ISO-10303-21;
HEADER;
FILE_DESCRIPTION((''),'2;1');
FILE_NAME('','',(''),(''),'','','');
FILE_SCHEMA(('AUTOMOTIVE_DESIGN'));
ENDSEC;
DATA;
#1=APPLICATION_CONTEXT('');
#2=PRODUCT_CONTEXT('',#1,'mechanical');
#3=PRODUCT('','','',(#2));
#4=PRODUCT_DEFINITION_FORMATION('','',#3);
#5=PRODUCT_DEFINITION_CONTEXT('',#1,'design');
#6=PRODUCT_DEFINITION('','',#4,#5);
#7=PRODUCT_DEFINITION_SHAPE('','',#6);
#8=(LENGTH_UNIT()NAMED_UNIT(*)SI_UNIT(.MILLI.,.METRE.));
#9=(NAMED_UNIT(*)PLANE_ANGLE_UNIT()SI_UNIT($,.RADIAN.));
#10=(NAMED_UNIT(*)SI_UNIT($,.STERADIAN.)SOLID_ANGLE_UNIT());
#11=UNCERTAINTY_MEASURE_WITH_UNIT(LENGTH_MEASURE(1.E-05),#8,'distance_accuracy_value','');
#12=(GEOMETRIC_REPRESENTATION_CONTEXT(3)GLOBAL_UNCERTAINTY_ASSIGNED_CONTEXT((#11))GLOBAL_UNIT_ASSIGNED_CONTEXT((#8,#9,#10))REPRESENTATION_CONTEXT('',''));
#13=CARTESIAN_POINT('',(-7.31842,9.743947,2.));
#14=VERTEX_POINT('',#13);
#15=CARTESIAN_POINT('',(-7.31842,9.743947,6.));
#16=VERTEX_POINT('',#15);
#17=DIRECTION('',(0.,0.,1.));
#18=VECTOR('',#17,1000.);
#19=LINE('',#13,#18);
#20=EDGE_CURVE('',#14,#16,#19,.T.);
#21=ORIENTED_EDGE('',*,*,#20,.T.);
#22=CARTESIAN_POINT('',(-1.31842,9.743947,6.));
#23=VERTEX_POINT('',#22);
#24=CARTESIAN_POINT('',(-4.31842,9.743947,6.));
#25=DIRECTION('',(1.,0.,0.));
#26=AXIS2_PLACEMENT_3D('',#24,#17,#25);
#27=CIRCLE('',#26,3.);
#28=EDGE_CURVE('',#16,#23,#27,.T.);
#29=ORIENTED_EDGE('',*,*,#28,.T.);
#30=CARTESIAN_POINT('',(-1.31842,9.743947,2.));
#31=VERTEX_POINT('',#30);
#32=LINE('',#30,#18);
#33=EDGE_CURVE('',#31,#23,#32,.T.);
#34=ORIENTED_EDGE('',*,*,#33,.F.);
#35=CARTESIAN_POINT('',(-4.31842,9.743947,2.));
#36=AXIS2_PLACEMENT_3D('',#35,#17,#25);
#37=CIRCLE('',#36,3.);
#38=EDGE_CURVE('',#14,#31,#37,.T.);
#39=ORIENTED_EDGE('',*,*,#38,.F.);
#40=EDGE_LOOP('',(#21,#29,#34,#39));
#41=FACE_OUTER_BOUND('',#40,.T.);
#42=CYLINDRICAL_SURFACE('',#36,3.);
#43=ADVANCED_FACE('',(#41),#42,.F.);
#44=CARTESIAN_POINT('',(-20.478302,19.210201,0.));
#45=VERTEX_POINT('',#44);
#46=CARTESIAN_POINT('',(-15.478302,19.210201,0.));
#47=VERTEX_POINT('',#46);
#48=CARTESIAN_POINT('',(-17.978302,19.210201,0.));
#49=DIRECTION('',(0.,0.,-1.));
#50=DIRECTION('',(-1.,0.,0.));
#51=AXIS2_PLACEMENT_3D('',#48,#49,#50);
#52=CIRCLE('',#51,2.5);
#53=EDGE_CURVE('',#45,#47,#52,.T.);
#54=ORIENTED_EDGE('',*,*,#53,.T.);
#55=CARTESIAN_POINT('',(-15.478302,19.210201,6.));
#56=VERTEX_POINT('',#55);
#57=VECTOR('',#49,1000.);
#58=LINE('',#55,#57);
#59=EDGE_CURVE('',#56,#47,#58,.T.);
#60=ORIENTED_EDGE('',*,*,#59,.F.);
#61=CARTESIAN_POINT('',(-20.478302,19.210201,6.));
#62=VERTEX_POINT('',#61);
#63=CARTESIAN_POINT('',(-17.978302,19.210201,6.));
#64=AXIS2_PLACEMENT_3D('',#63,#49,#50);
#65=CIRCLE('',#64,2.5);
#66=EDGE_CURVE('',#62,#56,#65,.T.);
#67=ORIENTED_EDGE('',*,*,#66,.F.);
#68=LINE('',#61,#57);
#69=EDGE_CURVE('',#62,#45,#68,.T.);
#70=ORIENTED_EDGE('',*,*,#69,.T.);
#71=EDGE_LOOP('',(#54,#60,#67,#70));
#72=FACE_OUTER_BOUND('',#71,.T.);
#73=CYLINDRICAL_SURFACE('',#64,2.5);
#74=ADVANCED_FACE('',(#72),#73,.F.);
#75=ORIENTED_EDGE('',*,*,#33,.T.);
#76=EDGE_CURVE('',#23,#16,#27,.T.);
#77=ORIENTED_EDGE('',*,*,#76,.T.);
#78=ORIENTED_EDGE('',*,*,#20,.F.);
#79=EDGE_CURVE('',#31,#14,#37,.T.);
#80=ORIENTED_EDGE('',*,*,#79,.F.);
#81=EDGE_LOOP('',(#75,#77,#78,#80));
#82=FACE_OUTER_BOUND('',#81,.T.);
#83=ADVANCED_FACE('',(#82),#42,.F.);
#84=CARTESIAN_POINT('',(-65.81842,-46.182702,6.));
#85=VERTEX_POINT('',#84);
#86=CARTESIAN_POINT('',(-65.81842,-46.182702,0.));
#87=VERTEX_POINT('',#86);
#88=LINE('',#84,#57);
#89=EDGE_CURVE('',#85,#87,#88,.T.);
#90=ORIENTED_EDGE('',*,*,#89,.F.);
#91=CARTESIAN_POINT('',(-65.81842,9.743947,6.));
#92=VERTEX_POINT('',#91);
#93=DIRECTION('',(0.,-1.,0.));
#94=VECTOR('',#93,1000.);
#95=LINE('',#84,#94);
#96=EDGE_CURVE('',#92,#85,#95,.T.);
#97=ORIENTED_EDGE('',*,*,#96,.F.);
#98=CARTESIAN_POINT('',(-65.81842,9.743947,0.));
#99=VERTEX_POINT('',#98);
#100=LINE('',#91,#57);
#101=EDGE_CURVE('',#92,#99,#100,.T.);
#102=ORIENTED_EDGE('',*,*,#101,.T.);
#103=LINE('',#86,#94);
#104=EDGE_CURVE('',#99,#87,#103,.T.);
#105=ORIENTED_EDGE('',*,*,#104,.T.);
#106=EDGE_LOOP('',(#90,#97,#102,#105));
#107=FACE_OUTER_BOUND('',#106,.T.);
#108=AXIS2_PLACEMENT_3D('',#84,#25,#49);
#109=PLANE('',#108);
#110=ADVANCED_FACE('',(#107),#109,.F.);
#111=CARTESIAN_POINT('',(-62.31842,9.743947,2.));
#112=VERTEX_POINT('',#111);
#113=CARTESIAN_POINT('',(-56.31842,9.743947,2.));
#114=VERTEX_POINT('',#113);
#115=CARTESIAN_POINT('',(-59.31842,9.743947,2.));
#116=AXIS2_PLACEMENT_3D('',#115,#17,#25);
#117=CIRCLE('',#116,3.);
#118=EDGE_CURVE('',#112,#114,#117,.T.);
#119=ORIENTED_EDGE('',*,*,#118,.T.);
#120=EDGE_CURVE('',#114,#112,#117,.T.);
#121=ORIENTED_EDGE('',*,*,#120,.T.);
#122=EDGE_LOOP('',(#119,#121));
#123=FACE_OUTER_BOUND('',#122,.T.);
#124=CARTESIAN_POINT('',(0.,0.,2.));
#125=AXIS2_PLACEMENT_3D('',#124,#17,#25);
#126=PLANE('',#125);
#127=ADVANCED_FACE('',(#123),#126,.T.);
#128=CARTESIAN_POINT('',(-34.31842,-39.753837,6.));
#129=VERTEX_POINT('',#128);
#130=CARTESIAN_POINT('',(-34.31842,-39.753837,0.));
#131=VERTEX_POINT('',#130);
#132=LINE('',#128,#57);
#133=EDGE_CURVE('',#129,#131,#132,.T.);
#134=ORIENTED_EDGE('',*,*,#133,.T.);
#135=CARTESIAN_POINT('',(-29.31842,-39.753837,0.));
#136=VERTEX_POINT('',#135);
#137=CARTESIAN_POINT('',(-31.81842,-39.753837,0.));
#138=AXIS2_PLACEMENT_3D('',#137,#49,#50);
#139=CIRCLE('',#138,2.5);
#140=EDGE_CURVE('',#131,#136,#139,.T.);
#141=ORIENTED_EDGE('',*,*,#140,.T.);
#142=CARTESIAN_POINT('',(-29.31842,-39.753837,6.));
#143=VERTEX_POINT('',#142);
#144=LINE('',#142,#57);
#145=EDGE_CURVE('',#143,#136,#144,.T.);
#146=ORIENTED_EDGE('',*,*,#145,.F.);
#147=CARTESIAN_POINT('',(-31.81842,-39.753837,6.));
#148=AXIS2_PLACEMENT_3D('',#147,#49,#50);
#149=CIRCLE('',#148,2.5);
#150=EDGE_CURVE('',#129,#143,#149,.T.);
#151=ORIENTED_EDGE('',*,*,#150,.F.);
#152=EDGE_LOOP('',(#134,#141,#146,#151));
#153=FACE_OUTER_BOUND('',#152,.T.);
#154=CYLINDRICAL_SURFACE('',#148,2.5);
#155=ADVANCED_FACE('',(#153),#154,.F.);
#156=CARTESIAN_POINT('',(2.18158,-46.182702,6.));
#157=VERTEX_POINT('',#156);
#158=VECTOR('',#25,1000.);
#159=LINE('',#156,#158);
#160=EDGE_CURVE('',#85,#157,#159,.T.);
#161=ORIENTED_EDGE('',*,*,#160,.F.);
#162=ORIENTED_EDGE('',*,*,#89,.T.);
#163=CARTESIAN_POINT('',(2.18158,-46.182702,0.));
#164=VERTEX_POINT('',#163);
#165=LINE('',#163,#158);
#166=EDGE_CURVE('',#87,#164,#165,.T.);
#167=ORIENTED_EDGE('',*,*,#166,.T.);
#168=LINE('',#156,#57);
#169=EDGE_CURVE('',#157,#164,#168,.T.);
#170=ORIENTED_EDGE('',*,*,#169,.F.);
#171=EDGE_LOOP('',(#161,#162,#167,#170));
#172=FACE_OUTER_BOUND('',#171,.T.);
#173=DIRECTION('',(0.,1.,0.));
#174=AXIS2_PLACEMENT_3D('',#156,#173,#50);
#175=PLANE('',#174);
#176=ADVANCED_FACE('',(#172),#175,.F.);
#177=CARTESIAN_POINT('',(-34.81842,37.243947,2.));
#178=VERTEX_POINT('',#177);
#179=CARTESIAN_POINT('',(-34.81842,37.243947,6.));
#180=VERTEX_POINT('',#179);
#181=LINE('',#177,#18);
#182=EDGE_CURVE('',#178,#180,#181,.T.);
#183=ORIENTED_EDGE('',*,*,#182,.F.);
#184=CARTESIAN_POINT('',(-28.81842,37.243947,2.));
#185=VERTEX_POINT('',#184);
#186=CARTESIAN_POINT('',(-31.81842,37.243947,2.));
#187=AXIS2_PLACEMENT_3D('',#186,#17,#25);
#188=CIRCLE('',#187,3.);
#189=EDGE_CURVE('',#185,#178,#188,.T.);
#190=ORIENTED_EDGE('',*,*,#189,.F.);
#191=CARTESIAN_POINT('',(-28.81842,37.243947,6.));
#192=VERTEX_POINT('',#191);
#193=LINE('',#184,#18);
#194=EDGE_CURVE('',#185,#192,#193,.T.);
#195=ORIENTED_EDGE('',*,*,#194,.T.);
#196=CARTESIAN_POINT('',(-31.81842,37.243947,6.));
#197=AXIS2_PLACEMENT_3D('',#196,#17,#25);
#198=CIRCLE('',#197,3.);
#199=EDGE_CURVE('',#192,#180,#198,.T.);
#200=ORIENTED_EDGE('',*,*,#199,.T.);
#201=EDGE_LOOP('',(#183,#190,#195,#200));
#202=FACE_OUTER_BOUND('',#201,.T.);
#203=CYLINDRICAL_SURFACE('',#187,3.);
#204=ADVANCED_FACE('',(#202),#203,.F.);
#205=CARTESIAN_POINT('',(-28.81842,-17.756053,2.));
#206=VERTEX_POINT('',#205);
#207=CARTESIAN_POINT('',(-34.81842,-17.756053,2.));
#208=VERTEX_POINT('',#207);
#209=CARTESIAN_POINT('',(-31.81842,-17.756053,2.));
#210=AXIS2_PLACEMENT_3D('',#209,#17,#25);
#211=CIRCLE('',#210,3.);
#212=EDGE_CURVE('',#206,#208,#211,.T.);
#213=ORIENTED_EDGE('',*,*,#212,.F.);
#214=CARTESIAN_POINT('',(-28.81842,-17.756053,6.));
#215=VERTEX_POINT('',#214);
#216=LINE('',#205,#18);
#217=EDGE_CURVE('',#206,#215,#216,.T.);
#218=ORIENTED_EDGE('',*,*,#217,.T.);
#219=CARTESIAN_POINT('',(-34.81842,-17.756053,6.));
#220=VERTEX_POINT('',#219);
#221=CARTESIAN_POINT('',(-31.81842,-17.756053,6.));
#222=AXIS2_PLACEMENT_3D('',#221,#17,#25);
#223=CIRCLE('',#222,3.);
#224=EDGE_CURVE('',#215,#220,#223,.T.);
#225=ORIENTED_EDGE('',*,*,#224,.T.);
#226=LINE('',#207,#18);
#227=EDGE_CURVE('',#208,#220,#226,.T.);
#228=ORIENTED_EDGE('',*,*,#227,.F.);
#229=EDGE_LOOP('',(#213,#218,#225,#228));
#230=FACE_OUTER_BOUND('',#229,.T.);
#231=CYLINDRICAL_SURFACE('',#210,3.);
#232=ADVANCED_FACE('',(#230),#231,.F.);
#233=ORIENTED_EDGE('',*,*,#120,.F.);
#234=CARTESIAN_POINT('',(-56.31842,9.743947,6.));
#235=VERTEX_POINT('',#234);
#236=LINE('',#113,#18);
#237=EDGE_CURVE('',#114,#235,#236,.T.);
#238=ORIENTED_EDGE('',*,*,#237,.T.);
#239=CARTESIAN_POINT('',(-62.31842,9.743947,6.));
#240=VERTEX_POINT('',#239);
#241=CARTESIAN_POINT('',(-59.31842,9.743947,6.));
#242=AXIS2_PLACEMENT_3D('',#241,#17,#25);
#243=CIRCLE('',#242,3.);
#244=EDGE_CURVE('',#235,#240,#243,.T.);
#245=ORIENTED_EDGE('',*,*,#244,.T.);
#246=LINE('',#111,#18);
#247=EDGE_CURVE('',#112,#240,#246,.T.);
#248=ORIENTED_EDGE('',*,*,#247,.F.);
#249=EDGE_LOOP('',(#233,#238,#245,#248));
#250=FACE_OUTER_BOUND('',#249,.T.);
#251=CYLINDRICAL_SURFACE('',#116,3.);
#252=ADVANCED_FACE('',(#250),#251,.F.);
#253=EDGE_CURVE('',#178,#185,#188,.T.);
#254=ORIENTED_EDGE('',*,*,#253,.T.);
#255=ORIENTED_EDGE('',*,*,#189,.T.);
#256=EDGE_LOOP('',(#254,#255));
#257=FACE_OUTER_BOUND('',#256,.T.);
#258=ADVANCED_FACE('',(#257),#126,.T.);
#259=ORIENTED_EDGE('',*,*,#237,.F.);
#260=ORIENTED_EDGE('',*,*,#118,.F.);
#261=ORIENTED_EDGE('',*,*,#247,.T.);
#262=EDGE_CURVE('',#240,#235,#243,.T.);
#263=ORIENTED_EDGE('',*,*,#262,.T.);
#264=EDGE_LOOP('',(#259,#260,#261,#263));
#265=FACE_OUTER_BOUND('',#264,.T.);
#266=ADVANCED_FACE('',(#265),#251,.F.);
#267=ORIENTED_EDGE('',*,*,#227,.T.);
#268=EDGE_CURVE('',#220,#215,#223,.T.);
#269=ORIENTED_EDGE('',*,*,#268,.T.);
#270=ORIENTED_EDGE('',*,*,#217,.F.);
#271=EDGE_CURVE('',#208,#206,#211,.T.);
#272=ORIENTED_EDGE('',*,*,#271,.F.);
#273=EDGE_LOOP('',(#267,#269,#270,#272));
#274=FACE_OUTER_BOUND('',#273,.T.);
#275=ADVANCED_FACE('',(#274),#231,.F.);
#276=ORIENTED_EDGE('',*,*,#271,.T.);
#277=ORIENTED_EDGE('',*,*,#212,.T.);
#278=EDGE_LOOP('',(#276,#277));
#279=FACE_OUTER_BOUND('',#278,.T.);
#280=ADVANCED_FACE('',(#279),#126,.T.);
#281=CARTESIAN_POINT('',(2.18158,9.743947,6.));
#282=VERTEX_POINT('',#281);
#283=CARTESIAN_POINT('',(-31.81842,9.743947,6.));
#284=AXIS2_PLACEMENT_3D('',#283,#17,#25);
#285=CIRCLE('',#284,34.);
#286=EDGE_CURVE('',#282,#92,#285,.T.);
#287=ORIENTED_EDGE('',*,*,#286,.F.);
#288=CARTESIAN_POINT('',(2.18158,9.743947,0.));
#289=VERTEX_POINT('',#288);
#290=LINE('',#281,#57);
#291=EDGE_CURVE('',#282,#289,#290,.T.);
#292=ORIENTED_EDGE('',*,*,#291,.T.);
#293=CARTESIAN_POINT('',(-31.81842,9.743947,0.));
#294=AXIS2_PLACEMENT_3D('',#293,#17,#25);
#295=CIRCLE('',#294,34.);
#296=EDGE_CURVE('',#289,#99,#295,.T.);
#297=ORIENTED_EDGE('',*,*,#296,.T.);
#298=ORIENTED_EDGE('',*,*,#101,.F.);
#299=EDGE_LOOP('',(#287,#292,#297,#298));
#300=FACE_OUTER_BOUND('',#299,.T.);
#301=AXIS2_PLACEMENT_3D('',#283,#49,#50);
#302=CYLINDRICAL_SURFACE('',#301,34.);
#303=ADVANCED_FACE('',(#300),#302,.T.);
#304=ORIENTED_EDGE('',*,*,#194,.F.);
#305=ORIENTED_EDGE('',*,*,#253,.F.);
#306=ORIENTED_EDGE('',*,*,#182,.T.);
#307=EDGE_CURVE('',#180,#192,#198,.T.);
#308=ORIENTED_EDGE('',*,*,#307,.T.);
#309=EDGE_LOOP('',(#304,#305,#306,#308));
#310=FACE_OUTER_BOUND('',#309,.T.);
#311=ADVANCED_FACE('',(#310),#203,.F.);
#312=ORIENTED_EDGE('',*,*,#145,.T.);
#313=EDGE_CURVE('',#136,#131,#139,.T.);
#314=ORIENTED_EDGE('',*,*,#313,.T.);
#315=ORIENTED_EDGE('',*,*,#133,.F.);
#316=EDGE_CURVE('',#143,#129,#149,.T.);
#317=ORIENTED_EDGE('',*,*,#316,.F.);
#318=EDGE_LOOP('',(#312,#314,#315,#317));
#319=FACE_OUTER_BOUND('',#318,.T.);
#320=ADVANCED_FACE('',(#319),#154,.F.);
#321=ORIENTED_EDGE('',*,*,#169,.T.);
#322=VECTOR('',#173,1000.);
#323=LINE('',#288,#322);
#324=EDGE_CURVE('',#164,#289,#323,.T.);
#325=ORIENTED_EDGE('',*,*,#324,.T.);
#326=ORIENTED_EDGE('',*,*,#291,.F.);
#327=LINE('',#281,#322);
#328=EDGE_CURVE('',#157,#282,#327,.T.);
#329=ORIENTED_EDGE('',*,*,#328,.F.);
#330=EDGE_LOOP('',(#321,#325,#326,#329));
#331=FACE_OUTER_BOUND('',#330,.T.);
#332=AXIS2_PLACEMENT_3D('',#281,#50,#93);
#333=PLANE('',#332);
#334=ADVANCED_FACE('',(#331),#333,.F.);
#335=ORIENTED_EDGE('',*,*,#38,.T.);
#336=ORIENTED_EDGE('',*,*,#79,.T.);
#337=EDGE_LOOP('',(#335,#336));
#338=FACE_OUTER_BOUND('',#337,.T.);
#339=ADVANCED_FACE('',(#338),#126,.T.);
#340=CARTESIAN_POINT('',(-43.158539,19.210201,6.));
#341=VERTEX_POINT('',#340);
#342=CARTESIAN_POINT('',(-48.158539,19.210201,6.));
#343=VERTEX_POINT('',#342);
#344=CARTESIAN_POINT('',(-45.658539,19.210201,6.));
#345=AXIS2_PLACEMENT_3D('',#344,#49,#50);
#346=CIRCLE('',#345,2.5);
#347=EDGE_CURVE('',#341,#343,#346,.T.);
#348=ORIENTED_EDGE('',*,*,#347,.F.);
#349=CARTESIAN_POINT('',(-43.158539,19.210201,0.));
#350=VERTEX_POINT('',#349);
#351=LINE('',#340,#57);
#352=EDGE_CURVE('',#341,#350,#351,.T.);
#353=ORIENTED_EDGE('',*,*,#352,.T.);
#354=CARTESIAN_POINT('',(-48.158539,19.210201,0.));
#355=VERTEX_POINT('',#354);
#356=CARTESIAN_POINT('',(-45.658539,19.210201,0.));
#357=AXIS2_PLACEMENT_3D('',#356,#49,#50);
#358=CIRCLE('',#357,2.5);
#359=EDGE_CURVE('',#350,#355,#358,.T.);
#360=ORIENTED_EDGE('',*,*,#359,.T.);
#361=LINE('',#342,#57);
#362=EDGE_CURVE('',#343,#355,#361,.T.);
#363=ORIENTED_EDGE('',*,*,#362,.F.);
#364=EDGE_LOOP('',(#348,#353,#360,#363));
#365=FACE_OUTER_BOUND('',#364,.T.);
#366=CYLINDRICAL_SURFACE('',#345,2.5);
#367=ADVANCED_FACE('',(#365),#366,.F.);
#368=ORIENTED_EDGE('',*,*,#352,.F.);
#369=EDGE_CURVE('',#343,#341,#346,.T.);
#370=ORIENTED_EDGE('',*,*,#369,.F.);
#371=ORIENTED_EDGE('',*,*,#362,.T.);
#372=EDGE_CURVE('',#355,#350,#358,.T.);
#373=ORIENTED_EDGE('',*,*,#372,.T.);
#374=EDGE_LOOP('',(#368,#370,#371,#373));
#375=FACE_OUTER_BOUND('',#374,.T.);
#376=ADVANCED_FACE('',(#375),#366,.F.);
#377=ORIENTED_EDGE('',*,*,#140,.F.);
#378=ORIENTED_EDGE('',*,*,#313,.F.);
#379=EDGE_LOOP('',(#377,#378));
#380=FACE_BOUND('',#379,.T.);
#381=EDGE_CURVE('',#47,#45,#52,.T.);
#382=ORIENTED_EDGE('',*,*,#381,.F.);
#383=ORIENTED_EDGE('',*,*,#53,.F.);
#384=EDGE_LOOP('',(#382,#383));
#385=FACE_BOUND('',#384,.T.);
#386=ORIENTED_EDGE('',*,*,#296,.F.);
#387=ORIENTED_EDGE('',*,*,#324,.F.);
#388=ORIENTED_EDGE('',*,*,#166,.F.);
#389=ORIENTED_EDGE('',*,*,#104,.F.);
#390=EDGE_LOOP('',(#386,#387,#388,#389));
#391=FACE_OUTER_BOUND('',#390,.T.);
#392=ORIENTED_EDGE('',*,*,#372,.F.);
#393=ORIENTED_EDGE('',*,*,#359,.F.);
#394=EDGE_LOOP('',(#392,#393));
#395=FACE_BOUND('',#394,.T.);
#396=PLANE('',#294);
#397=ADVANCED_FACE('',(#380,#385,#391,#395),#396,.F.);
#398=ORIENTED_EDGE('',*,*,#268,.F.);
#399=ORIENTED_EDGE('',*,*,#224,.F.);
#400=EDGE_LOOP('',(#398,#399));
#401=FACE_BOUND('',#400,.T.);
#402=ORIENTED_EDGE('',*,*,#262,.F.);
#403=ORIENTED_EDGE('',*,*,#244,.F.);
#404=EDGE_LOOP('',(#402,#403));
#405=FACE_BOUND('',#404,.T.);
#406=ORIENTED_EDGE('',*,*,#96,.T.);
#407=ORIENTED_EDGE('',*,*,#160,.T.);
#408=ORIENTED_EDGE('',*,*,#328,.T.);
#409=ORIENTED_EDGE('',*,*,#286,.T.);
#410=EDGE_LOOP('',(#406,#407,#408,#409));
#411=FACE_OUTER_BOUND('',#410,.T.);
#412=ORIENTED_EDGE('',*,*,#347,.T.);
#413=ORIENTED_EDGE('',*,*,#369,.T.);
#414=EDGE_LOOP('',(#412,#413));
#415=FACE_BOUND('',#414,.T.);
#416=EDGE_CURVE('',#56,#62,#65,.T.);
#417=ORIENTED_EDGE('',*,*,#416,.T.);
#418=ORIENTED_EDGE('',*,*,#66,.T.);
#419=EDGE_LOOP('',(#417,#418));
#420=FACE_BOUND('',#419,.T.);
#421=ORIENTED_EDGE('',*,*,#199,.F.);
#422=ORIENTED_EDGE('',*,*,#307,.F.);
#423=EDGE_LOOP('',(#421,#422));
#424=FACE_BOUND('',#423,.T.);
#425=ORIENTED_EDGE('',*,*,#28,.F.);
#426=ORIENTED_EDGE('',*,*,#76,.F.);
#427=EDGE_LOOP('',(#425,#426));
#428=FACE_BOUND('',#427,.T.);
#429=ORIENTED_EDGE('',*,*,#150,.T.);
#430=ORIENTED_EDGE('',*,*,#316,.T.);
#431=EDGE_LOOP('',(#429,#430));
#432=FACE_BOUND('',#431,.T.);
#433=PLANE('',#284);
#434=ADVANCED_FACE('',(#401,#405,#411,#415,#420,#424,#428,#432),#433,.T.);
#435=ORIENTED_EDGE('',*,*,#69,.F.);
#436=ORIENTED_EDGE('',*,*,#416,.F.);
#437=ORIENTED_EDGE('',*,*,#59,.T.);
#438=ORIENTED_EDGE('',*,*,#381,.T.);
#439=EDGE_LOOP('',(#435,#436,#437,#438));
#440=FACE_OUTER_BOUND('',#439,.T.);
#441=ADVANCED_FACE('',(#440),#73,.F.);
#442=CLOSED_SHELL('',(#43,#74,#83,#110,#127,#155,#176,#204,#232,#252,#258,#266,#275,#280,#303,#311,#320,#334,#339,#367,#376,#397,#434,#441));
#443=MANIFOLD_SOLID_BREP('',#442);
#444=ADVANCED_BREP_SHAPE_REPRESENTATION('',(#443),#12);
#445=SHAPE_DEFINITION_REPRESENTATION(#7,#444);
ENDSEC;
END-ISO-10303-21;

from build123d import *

# Parameters (mm, degrees)
BOSS_EXTRUDE1_DEPTH = 6
SKETCH3_R           = 3
CUT_EXTRUDE1_DEPTH  = 4
SKETCH9_R           = 2.5
CUT_EXTRUDE2_DEPTH  = 6


with BuildPart() as part:
    # Sketch2 → Boss-Extrude1 (new body)
    with BuildSketch(Plane.XY):
        with BuildLine():
            Line((2.181579686, 9.743947498), (2.181579686, -46.182702418))
            Line((2.181579686, -46.182702418), (-65.818420314, -46.182702418))
            Line((-65.818420314, -46.182702418), (-65.818420314, 9.743947498))
            ThreePointArc((-65.818420314, 9.743947498), (-31.818420314, 43.743947498), (2.181579686, 9.743947498))
        make_face()
    extrude(amount=BOSS_EXTRUDE1_DEPTH)

    # Sketch3 → Cut-Extrude1 (cut)
    with BuildSketch(Plane.XY.offset(6)):
        with Locations((-4.318420314, 9.743947498)):
            Circle(SKETCH3_R)
        with Locations((-31.818420314, -17.756052502)):
            Circle(SKETCH3_R)
        with Locations((-59.318420314, 9.743947498)):
            Circle(SKETCH3_R)
        with Locations((-31.818420314, 37.243947498)):
            Circle(SKETCH3_R)
    extrude(amount=-CUT_EXTRUDE1_DEPTH, mode=Mode.SUBTRACT)

    # Sketch9 → Cut-Extrude2 (cut)
    with BuildSketch(Plane(origin=(0, 0, 0), x_dir=(-1, 0, 0), z_dir=(0, 0, -1))):
        with Locations((45.658538984, 19.210200864)):
            Circle(SKETCH9_R)
        with Locations((17.978301644, 19.210200864)):
            Circle(SKETCH9_R)
        with Locations((31.818420314, -39.753837028)):
            Circle(SKETCH9_R)
    extrude(amount=-CUT_EXTRUDE2_DEPTH, mode=Mode.SUBTRACT)


solid = part.part
